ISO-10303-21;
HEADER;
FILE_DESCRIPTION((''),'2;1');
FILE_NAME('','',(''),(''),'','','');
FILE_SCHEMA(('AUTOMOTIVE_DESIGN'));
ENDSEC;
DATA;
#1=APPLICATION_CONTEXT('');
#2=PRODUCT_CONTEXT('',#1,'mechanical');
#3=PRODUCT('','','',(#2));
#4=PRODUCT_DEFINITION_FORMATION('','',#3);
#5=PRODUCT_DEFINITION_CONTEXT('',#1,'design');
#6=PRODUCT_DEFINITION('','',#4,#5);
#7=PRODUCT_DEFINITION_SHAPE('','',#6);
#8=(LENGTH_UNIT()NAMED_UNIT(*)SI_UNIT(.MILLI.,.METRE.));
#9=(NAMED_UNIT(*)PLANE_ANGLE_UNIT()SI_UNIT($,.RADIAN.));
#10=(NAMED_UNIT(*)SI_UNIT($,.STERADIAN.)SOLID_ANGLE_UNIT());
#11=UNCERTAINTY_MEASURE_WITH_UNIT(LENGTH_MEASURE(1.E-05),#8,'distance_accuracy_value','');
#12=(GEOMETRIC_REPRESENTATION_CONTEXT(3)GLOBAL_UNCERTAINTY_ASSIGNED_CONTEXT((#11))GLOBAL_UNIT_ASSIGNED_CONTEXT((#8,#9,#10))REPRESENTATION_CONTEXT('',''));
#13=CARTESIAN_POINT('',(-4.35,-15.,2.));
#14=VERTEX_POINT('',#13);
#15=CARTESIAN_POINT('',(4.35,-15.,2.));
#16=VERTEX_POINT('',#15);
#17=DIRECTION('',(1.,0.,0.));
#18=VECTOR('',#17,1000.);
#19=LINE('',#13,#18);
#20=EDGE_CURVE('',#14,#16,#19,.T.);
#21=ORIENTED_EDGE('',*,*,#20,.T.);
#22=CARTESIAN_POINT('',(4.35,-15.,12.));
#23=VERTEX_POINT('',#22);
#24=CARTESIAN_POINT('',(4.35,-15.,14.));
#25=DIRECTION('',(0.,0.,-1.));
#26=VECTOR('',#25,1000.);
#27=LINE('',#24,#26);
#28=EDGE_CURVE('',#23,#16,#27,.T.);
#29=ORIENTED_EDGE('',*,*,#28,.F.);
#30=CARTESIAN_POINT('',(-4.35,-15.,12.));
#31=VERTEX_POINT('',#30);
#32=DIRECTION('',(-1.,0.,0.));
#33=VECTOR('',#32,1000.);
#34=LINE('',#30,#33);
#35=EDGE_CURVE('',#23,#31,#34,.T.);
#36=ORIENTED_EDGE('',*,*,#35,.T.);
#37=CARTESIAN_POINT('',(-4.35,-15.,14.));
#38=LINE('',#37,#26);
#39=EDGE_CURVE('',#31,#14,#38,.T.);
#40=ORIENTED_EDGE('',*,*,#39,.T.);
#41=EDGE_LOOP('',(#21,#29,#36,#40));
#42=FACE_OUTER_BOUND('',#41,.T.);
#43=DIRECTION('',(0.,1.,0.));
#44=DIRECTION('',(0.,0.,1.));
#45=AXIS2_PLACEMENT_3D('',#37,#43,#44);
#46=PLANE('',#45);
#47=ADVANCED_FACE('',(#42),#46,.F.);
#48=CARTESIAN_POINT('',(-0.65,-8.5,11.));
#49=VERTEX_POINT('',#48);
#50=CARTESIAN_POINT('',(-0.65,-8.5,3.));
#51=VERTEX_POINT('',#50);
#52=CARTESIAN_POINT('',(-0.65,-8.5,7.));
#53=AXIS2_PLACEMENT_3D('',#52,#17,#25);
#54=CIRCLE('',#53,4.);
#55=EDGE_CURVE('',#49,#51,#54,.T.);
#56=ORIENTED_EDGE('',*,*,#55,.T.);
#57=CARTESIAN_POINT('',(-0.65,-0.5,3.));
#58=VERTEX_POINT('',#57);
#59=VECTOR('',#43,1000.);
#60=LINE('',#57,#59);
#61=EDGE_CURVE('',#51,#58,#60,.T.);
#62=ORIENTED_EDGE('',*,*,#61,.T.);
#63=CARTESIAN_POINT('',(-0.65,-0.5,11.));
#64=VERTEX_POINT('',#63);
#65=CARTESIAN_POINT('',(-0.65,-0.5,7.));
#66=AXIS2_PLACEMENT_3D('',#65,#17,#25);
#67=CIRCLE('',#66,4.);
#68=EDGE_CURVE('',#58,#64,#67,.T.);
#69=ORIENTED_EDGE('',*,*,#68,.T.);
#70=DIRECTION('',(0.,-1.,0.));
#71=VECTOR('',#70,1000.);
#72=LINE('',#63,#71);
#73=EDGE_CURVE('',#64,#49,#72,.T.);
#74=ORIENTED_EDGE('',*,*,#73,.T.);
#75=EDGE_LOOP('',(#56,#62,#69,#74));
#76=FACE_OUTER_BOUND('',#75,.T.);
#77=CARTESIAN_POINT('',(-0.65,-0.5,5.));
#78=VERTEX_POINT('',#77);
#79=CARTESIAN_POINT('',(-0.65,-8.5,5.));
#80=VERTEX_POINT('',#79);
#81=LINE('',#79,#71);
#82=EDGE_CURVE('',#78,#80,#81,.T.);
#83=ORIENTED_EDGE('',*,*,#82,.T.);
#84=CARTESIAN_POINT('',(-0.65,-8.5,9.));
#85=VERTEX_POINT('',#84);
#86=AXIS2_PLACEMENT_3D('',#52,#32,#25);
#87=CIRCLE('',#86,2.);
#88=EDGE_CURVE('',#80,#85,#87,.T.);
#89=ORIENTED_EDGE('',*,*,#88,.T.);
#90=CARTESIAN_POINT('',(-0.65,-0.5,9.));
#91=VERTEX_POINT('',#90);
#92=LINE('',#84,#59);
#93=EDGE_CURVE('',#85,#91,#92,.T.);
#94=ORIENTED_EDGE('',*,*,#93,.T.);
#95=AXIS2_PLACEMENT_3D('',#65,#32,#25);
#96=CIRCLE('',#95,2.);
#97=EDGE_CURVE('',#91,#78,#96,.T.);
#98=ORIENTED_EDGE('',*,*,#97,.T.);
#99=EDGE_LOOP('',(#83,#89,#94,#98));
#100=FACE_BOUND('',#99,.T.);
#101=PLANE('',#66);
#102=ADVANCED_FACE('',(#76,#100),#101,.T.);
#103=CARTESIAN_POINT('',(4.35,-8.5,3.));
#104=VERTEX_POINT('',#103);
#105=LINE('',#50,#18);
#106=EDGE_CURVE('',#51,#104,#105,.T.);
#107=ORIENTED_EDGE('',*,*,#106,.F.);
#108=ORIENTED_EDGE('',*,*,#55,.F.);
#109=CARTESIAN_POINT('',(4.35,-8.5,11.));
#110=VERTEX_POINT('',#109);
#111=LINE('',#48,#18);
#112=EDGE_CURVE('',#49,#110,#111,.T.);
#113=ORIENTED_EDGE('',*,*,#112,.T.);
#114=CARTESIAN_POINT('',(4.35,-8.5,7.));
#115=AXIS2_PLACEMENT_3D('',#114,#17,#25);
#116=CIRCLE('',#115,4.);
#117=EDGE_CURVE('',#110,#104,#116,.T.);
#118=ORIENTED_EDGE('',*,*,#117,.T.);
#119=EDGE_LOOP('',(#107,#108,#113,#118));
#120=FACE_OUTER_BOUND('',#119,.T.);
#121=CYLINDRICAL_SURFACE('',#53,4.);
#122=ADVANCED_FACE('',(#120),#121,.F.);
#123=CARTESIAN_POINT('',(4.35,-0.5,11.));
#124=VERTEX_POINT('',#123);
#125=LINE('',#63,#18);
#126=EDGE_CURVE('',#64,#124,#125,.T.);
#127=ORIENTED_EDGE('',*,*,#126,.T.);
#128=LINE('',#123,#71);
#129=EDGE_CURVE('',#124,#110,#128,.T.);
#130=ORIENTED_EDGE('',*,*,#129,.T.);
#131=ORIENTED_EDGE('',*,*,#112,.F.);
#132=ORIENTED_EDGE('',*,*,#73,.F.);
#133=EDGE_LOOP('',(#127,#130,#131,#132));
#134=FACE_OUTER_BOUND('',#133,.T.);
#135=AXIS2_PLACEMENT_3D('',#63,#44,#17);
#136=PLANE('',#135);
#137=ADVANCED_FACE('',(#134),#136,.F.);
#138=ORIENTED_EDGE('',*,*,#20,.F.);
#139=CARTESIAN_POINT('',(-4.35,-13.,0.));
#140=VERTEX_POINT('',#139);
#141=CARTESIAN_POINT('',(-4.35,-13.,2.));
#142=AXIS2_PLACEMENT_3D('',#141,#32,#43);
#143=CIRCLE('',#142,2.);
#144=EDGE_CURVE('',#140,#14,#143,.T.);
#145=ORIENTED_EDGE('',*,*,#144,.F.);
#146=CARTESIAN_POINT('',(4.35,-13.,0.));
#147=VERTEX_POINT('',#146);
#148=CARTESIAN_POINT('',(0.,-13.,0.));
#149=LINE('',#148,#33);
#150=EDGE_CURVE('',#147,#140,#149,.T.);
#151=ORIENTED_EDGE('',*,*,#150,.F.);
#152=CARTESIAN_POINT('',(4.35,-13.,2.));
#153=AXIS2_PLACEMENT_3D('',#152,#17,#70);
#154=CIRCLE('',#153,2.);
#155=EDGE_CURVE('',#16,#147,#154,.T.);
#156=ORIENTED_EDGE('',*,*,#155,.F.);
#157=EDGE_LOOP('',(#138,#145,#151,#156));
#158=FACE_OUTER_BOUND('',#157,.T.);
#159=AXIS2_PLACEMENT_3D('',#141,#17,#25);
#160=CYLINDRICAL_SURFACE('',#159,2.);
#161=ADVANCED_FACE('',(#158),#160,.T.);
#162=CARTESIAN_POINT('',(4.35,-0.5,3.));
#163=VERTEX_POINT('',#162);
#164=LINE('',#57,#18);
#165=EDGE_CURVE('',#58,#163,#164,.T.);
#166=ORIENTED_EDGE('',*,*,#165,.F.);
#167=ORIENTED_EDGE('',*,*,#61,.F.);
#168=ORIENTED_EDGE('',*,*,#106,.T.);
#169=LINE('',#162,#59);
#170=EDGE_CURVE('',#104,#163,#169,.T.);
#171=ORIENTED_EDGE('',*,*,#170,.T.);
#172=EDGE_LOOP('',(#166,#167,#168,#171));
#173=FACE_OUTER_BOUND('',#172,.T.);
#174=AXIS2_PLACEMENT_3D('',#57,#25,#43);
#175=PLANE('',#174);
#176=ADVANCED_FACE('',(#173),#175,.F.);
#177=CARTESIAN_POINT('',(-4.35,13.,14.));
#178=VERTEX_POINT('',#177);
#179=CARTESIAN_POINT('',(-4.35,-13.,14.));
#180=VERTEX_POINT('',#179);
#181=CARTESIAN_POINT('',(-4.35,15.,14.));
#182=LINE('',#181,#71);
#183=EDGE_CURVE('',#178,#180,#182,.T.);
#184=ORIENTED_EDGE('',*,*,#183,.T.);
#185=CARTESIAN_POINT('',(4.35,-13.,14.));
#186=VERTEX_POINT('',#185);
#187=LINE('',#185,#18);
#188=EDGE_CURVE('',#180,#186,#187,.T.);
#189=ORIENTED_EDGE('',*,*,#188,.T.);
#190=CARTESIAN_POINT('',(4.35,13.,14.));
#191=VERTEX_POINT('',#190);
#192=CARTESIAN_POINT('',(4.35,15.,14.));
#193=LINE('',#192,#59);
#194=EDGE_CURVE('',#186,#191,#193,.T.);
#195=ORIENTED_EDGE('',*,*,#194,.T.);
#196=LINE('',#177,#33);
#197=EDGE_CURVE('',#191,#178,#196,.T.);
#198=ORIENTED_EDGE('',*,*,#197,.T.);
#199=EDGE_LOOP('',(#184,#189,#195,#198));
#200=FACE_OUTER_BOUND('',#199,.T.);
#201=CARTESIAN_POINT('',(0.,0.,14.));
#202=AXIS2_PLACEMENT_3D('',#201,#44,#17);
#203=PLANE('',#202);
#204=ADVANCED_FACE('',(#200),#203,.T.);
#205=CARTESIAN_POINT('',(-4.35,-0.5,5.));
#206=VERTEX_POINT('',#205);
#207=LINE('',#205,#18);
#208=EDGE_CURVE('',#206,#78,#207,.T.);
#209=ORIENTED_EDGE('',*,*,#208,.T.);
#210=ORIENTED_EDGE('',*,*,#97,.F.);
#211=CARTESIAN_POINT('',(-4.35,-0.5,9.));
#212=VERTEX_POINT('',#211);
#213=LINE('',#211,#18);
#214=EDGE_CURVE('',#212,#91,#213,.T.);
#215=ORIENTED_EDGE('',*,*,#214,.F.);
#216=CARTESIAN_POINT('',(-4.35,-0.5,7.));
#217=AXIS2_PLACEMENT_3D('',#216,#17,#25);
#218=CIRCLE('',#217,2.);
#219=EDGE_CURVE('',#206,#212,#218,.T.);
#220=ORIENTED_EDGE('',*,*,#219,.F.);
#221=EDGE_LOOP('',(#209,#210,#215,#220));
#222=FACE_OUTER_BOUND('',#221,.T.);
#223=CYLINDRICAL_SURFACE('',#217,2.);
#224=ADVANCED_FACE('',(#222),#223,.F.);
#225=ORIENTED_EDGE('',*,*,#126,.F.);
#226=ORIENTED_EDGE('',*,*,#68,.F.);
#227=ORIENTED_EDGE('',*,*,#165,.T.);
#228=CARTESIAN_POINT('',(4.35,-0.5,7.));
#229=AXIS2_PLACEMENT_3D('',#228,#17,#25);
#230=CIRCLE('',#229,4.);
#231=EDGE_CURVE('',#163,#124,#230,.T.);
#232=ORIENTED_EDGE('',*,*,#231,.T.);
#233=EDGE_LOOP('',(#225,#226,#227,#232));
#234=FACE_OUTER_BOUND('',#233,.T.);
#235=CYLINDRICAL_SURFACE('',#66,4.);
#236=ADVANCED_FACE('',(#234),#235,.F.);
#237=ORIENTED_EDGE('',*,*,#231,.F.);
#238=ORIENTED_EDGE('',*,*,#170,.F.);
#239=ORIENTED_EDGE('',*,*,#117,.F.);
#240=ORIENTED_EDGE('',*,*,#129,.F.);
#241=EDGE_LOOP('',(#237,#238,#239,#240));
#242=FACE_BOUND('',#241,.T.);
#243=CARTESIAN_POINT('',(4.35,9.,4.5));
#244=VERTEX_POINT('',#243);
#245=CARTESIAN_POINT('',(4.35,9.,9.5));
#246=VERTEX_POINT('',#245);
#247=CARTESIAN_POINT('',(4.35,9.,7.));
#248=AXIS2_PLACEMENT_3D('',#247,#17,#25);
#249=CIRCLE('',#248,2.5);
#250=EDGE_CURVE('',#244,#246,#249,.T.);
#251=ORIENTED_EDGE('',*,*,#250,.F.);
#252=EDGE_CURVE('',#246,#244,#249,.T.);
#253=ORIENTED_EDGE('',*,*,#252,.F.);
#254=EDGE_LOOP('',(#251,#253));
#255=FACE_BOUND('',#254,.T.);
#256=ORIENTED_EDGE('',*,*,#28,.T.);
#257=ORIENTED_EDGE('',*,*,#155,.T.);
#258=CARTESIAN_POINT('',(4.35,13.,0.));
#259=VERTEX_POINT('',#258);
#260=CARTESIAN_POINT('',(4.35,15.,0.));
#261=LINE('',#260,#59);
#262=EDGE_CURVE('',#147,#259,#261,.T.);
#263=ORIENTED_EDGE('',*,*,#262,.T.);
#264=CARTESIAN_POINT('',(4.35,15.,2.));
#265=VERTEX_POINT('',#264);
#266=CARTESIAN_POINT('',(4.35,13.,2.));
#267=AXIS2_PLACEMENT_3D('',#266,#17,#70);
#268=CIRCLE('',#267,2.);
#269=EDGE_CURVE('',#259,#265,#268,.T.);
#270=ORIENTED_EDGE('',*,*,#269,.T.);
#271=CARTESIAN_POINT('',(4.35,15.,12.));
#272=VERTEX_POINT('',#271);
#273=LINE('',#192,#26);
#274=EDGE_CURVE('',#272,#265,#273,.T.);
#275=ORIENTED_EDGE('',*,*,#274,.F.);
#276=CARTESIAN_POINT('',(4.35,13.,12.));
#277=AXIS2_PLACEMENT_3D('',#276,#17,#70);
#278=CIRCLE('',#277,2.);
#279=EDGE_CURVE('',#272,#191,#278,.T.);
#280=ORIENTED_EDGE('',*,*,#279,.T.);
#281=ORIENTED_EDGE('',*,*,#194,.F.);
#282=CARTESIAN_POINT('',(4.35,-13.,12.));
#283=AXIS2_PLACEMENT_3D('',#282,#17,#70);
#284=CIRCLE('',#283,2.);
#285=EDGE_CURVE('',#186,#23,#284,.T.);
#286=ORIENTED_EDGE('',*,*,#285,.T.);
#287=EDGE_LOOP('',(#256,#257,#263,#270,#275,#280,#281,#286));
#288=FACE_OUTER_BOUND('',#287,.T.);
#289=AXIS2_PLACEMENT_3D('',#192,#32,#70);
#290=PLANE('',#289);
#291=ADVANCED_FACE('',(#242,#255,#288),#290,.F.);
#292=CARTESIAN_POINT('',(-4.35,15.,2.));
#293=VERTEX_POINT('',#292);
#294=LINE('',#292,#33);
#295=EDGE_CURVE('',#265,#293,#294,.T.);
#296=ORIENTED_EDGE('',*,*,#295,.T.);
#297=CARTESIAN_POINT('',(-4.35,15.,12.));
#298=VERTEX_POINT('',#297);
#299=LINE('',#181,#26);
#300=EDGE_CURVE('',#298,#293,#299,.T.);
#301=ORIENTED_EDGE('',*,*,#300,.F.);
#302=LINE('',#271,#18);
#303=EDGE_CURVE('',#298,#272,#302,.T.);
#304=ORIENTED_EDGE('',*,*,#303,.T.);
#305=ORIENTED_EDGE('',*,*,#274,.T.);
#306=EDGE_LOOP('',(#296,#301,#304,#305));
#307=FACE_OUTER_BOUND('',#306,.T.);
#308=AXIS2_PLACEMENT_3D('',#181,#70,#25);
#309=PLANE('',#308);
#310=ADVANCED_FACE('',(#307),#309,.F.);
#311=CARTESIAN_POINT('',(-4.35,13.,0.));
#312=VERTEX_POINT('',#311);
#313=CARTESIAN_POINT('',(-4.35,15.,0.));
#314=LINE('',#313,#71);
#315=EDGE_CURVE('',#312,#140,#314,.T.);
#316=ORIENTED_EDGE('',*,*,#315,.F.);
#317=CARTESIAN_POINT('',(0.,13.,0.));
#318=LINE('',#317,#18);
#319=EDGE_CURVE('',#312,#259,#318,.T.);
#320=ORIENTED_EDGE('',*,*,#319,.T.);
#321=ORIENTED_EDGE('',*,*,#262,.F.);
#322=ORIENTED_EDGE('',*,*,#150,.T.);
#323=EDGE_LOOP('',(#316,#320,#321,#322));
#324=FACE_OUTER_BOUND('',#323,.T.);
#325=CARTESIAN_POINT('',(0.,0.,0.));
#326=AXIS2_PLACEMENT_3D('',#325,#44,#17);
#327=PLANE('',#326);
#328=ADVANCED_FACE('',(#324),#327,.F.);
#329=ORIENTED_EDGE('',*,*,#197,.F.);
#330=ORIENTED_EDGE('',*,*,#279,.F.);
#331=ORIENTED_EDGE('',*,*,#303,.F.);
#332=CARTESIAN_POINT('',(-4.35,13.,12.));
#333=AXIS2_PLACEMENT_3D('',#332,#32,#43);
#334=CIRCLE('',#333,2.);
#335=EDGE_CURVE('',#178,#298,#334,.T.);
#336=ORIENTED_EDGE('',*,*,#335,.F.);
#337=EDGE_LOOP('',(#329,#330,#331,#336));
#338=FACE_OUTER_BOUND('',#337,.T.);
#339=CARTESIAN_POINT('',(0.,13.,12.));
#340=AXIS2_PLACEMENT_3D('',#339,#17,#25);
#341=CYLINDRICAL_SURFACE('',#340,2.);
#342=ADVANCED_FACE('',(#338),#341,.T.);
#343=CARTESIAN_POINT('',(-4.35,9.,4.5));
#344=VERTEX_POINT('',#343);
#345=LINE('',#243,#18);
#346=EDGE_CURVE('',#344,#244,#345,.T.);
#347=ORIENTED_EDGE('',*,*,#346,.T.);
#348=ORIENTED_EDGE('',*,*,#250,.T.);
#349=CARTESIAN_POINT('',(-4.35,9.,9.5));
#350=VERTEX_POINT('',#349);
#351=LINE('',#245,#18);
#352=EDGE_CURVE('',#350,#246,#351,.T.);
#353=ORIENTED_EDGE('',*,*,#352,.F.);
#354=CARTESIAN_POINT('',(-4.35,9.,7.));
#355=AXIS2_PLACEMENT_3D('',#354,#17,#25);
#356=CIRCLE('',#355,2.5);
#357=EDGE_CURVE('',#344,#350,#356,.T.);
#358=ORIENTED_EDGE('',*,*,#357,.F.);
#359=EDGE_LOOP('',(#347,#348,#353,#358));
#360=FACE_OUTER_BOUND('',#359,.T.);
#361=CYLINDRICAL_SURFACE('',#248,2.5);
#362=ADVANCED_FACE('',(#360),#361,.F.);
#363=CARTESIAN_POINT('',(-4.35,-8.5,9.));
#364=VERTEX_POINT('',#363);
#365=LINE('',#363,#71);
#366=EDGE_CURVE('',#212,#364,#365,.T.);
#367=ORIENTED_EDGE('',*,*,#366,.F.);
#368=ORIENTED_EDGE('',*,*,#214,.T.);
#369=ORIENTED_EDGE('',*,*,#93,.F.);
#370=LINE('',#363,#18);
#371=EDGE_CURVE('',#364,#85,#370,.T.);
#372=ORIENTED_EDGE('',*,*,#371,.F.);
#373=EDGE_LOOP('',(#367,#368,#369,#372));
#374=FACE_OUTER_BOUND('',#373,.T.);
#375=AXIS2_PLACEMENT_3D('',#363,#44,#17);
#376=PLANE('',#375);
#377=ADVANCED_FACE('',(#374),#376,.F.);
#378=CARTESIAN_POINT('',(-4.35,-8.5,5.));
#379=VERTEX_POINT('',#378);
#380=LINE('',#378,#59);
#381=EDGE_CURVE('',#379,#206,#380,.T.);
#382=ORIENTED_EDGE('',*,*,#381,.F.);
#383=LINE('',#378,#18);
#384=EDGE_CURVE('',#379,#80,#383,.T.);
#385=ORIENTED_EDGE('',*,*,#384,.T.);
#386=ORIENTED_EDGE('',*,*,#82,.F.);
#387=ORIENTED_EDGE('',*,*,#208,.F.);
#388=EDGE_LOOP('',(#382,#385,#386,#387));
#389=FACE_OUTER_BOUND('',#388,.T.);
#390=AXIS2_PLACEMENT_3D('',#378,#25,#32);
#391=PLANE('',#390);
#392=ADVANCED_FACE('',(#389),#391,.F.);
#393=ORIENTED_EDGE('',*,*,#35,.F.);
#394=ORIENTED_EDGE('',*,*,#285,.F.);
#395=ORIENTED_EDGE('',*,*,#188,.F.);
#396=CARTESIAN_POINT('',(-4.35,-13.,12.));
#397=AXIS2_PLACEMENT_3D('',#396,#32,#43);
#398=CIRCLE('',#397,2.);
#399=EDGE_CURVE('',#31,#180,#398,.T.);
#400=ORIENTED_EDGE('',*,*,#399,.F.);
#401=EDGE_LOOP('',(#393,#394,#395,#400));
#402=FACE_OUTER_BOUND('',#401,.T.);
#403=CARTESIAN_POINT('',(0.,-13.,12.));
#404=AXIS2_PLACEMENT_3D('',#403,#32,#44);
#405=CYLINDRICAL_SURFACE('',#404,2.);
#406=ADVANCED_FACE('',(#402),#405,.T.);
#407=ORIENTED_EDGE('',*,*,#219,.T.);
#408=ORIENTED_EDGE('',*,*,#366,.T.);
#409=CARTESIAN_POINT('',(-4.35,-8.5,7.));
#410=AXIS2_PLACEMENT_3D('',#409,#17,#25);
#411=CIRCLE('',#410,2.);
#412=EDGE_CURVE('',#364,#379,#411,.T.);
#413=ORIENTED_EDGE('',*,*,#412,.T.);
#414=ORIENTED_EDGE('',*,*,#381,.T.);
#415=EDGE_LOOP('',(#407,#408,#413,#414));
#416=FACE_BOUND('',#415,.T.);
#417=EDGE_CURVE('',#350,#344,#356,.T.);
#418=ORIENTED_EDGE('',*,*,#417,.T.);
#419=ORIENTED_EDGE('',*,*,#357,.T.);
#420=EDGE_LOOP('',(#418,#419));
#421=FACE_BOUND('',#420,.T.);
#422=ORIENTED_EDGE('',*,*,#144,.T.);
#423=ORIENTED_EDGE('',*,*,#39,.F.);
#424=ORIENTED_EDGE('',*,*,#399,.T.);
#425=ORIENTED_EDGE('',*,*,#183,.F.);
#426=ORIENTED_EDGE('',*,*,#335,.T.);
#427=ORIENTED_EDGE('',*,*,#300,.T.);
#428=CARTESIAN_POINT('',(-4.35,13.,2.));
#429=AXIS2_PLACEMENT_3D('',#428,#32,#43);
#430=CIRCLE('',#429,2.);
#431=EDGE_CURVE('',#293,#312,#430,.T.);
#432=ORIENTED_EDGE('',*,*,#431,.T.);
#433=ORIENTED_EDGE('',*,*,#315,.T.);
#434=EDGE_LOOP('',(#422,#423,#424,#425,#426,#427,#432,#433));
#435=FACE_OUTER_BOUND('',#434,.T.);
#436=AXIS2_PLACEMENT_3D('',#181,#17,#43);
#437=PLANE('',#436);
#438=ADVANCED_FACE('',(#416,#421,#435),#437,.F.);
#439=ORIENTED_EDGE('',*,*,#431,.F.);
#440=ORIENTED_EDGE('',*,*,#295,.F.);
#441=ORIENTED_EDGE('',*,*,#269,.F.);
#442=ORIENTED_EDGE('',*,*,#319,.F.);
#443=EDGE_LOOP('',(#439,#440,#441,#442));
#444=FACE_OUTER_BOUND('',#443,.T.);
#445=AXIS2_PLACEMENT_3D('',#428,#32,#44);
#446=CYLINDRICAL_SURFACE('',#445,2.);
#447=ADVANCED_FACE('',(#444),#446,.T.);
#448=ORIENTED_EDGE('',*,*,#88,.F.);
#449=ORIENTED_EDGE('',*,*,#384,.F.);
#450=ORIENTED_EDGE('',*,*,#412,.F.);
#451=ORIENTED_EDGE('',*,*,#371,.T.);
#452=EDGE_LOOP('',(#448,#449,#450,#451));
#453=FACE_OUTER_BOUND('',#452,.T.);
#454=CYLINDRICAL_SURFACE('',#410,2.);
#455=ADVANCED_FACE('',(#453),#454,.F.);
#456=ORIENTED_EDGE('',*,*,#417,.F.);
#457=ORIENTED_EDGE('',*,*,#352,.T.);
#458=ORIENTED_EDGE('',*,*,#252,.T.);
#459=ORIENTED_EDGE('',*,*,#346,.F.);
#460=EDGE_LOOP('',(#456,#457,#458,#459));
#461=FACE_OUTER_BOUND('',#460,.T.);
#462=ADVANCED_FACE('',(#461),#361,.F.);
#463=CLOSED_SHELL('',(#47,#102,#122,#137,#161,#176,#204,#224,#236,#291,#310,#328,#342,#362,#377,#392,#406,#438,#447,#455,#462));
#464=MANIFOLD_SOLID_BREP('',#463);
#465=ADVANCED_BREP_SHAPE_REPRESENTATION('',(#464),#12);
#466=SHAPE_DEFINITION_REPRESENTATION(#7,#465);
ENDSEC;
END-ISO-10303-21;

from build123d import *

# Parameters (mm, degrees)
SKETCH_1_W          = 8.7
SKETCH_1_H          = 30
EXTRUDE_1_DEPTH     = 14
HOLE_WIZARD_M6_1_D  = 5
CUT_EXTRUDE_1_DEPTH = 23.286543025
CUT_EXTRUDE_2_DEPTH = 5
FILLET_1_R          = 2


with BuildPart() as part:
    # 草图1 → 凸台-拉伸1 (new body)
    with BuildSketch(Plane.XY):
        Rectangle(SKETCH_1_W, SKETCH_1_H)
    extrude(amount=EXTRUDE_1_DEPTH)

    # M6 螺纹孔1 (through all)
    with Locations(Plane(origin=(4.35, 0, 0), x_dir=(0, 0, -1), z_dir=(1, 0, 0))):
        with Locations((-7, 9)):
            Hole(HOLE_WIZARD_M6_1_D / 2)

    # 草图4 → 切除-拉伸1 (cut, through all)
    with BuildSketch(Plane(origin=(4.35, 0, 0), x_dir=(0, 0, -1), z_dir=(1, 0, 0))):
        with BuildLine():
            Line((-9, -8.5), (-9, -0.5))
            ThreePointArc((-9, -0.5), (-7, 1.5), (-5, -0.5))
            Line((-5, -0.5), (-5, -8.5))
            ThreePointArc((-5, -8.5), (-7, -10.5), (-9, -8.5))
        make_face()
    extrude(amount=-CUT_EXTRUDE_1_DEPTH, mode=Mode.SUBTRACT)

    # 草图5 → 切除-拉伸2 (cut)
    with BuildSketch(Plane(origin=(4.35, 0, 0), x_dir=(0, 0, -1), z_dir=(1, 0, 0))):
        with BuildLine():
            Line((-3, -0.5), (-3, -8.5))
            ThreePointArc((-3, -8.5), (-7, -12.5), (-11, -8.5))
            Line((-11, -8.5), (-11, -0.5))
            ThreePointArc((-11, -0.5), (-7, 3.5), (-3, -0.5))
        make_face()
    extrude(amount=-CUT_EXTRUDE_2_DEPTH, mode=Mode.SUBTRACT)

    # 圆角1
    fillet_1_edges = [part.edges().sort_by_distance(p)[0] for p in [
        (0, -15, 14),
        (0, -15, 0),
        (0, 15, 0),
        (0, 15, 14),
    ]]
    fillet(fillet_1_edges, radius=FILLET_1_R)


solid = part.part
